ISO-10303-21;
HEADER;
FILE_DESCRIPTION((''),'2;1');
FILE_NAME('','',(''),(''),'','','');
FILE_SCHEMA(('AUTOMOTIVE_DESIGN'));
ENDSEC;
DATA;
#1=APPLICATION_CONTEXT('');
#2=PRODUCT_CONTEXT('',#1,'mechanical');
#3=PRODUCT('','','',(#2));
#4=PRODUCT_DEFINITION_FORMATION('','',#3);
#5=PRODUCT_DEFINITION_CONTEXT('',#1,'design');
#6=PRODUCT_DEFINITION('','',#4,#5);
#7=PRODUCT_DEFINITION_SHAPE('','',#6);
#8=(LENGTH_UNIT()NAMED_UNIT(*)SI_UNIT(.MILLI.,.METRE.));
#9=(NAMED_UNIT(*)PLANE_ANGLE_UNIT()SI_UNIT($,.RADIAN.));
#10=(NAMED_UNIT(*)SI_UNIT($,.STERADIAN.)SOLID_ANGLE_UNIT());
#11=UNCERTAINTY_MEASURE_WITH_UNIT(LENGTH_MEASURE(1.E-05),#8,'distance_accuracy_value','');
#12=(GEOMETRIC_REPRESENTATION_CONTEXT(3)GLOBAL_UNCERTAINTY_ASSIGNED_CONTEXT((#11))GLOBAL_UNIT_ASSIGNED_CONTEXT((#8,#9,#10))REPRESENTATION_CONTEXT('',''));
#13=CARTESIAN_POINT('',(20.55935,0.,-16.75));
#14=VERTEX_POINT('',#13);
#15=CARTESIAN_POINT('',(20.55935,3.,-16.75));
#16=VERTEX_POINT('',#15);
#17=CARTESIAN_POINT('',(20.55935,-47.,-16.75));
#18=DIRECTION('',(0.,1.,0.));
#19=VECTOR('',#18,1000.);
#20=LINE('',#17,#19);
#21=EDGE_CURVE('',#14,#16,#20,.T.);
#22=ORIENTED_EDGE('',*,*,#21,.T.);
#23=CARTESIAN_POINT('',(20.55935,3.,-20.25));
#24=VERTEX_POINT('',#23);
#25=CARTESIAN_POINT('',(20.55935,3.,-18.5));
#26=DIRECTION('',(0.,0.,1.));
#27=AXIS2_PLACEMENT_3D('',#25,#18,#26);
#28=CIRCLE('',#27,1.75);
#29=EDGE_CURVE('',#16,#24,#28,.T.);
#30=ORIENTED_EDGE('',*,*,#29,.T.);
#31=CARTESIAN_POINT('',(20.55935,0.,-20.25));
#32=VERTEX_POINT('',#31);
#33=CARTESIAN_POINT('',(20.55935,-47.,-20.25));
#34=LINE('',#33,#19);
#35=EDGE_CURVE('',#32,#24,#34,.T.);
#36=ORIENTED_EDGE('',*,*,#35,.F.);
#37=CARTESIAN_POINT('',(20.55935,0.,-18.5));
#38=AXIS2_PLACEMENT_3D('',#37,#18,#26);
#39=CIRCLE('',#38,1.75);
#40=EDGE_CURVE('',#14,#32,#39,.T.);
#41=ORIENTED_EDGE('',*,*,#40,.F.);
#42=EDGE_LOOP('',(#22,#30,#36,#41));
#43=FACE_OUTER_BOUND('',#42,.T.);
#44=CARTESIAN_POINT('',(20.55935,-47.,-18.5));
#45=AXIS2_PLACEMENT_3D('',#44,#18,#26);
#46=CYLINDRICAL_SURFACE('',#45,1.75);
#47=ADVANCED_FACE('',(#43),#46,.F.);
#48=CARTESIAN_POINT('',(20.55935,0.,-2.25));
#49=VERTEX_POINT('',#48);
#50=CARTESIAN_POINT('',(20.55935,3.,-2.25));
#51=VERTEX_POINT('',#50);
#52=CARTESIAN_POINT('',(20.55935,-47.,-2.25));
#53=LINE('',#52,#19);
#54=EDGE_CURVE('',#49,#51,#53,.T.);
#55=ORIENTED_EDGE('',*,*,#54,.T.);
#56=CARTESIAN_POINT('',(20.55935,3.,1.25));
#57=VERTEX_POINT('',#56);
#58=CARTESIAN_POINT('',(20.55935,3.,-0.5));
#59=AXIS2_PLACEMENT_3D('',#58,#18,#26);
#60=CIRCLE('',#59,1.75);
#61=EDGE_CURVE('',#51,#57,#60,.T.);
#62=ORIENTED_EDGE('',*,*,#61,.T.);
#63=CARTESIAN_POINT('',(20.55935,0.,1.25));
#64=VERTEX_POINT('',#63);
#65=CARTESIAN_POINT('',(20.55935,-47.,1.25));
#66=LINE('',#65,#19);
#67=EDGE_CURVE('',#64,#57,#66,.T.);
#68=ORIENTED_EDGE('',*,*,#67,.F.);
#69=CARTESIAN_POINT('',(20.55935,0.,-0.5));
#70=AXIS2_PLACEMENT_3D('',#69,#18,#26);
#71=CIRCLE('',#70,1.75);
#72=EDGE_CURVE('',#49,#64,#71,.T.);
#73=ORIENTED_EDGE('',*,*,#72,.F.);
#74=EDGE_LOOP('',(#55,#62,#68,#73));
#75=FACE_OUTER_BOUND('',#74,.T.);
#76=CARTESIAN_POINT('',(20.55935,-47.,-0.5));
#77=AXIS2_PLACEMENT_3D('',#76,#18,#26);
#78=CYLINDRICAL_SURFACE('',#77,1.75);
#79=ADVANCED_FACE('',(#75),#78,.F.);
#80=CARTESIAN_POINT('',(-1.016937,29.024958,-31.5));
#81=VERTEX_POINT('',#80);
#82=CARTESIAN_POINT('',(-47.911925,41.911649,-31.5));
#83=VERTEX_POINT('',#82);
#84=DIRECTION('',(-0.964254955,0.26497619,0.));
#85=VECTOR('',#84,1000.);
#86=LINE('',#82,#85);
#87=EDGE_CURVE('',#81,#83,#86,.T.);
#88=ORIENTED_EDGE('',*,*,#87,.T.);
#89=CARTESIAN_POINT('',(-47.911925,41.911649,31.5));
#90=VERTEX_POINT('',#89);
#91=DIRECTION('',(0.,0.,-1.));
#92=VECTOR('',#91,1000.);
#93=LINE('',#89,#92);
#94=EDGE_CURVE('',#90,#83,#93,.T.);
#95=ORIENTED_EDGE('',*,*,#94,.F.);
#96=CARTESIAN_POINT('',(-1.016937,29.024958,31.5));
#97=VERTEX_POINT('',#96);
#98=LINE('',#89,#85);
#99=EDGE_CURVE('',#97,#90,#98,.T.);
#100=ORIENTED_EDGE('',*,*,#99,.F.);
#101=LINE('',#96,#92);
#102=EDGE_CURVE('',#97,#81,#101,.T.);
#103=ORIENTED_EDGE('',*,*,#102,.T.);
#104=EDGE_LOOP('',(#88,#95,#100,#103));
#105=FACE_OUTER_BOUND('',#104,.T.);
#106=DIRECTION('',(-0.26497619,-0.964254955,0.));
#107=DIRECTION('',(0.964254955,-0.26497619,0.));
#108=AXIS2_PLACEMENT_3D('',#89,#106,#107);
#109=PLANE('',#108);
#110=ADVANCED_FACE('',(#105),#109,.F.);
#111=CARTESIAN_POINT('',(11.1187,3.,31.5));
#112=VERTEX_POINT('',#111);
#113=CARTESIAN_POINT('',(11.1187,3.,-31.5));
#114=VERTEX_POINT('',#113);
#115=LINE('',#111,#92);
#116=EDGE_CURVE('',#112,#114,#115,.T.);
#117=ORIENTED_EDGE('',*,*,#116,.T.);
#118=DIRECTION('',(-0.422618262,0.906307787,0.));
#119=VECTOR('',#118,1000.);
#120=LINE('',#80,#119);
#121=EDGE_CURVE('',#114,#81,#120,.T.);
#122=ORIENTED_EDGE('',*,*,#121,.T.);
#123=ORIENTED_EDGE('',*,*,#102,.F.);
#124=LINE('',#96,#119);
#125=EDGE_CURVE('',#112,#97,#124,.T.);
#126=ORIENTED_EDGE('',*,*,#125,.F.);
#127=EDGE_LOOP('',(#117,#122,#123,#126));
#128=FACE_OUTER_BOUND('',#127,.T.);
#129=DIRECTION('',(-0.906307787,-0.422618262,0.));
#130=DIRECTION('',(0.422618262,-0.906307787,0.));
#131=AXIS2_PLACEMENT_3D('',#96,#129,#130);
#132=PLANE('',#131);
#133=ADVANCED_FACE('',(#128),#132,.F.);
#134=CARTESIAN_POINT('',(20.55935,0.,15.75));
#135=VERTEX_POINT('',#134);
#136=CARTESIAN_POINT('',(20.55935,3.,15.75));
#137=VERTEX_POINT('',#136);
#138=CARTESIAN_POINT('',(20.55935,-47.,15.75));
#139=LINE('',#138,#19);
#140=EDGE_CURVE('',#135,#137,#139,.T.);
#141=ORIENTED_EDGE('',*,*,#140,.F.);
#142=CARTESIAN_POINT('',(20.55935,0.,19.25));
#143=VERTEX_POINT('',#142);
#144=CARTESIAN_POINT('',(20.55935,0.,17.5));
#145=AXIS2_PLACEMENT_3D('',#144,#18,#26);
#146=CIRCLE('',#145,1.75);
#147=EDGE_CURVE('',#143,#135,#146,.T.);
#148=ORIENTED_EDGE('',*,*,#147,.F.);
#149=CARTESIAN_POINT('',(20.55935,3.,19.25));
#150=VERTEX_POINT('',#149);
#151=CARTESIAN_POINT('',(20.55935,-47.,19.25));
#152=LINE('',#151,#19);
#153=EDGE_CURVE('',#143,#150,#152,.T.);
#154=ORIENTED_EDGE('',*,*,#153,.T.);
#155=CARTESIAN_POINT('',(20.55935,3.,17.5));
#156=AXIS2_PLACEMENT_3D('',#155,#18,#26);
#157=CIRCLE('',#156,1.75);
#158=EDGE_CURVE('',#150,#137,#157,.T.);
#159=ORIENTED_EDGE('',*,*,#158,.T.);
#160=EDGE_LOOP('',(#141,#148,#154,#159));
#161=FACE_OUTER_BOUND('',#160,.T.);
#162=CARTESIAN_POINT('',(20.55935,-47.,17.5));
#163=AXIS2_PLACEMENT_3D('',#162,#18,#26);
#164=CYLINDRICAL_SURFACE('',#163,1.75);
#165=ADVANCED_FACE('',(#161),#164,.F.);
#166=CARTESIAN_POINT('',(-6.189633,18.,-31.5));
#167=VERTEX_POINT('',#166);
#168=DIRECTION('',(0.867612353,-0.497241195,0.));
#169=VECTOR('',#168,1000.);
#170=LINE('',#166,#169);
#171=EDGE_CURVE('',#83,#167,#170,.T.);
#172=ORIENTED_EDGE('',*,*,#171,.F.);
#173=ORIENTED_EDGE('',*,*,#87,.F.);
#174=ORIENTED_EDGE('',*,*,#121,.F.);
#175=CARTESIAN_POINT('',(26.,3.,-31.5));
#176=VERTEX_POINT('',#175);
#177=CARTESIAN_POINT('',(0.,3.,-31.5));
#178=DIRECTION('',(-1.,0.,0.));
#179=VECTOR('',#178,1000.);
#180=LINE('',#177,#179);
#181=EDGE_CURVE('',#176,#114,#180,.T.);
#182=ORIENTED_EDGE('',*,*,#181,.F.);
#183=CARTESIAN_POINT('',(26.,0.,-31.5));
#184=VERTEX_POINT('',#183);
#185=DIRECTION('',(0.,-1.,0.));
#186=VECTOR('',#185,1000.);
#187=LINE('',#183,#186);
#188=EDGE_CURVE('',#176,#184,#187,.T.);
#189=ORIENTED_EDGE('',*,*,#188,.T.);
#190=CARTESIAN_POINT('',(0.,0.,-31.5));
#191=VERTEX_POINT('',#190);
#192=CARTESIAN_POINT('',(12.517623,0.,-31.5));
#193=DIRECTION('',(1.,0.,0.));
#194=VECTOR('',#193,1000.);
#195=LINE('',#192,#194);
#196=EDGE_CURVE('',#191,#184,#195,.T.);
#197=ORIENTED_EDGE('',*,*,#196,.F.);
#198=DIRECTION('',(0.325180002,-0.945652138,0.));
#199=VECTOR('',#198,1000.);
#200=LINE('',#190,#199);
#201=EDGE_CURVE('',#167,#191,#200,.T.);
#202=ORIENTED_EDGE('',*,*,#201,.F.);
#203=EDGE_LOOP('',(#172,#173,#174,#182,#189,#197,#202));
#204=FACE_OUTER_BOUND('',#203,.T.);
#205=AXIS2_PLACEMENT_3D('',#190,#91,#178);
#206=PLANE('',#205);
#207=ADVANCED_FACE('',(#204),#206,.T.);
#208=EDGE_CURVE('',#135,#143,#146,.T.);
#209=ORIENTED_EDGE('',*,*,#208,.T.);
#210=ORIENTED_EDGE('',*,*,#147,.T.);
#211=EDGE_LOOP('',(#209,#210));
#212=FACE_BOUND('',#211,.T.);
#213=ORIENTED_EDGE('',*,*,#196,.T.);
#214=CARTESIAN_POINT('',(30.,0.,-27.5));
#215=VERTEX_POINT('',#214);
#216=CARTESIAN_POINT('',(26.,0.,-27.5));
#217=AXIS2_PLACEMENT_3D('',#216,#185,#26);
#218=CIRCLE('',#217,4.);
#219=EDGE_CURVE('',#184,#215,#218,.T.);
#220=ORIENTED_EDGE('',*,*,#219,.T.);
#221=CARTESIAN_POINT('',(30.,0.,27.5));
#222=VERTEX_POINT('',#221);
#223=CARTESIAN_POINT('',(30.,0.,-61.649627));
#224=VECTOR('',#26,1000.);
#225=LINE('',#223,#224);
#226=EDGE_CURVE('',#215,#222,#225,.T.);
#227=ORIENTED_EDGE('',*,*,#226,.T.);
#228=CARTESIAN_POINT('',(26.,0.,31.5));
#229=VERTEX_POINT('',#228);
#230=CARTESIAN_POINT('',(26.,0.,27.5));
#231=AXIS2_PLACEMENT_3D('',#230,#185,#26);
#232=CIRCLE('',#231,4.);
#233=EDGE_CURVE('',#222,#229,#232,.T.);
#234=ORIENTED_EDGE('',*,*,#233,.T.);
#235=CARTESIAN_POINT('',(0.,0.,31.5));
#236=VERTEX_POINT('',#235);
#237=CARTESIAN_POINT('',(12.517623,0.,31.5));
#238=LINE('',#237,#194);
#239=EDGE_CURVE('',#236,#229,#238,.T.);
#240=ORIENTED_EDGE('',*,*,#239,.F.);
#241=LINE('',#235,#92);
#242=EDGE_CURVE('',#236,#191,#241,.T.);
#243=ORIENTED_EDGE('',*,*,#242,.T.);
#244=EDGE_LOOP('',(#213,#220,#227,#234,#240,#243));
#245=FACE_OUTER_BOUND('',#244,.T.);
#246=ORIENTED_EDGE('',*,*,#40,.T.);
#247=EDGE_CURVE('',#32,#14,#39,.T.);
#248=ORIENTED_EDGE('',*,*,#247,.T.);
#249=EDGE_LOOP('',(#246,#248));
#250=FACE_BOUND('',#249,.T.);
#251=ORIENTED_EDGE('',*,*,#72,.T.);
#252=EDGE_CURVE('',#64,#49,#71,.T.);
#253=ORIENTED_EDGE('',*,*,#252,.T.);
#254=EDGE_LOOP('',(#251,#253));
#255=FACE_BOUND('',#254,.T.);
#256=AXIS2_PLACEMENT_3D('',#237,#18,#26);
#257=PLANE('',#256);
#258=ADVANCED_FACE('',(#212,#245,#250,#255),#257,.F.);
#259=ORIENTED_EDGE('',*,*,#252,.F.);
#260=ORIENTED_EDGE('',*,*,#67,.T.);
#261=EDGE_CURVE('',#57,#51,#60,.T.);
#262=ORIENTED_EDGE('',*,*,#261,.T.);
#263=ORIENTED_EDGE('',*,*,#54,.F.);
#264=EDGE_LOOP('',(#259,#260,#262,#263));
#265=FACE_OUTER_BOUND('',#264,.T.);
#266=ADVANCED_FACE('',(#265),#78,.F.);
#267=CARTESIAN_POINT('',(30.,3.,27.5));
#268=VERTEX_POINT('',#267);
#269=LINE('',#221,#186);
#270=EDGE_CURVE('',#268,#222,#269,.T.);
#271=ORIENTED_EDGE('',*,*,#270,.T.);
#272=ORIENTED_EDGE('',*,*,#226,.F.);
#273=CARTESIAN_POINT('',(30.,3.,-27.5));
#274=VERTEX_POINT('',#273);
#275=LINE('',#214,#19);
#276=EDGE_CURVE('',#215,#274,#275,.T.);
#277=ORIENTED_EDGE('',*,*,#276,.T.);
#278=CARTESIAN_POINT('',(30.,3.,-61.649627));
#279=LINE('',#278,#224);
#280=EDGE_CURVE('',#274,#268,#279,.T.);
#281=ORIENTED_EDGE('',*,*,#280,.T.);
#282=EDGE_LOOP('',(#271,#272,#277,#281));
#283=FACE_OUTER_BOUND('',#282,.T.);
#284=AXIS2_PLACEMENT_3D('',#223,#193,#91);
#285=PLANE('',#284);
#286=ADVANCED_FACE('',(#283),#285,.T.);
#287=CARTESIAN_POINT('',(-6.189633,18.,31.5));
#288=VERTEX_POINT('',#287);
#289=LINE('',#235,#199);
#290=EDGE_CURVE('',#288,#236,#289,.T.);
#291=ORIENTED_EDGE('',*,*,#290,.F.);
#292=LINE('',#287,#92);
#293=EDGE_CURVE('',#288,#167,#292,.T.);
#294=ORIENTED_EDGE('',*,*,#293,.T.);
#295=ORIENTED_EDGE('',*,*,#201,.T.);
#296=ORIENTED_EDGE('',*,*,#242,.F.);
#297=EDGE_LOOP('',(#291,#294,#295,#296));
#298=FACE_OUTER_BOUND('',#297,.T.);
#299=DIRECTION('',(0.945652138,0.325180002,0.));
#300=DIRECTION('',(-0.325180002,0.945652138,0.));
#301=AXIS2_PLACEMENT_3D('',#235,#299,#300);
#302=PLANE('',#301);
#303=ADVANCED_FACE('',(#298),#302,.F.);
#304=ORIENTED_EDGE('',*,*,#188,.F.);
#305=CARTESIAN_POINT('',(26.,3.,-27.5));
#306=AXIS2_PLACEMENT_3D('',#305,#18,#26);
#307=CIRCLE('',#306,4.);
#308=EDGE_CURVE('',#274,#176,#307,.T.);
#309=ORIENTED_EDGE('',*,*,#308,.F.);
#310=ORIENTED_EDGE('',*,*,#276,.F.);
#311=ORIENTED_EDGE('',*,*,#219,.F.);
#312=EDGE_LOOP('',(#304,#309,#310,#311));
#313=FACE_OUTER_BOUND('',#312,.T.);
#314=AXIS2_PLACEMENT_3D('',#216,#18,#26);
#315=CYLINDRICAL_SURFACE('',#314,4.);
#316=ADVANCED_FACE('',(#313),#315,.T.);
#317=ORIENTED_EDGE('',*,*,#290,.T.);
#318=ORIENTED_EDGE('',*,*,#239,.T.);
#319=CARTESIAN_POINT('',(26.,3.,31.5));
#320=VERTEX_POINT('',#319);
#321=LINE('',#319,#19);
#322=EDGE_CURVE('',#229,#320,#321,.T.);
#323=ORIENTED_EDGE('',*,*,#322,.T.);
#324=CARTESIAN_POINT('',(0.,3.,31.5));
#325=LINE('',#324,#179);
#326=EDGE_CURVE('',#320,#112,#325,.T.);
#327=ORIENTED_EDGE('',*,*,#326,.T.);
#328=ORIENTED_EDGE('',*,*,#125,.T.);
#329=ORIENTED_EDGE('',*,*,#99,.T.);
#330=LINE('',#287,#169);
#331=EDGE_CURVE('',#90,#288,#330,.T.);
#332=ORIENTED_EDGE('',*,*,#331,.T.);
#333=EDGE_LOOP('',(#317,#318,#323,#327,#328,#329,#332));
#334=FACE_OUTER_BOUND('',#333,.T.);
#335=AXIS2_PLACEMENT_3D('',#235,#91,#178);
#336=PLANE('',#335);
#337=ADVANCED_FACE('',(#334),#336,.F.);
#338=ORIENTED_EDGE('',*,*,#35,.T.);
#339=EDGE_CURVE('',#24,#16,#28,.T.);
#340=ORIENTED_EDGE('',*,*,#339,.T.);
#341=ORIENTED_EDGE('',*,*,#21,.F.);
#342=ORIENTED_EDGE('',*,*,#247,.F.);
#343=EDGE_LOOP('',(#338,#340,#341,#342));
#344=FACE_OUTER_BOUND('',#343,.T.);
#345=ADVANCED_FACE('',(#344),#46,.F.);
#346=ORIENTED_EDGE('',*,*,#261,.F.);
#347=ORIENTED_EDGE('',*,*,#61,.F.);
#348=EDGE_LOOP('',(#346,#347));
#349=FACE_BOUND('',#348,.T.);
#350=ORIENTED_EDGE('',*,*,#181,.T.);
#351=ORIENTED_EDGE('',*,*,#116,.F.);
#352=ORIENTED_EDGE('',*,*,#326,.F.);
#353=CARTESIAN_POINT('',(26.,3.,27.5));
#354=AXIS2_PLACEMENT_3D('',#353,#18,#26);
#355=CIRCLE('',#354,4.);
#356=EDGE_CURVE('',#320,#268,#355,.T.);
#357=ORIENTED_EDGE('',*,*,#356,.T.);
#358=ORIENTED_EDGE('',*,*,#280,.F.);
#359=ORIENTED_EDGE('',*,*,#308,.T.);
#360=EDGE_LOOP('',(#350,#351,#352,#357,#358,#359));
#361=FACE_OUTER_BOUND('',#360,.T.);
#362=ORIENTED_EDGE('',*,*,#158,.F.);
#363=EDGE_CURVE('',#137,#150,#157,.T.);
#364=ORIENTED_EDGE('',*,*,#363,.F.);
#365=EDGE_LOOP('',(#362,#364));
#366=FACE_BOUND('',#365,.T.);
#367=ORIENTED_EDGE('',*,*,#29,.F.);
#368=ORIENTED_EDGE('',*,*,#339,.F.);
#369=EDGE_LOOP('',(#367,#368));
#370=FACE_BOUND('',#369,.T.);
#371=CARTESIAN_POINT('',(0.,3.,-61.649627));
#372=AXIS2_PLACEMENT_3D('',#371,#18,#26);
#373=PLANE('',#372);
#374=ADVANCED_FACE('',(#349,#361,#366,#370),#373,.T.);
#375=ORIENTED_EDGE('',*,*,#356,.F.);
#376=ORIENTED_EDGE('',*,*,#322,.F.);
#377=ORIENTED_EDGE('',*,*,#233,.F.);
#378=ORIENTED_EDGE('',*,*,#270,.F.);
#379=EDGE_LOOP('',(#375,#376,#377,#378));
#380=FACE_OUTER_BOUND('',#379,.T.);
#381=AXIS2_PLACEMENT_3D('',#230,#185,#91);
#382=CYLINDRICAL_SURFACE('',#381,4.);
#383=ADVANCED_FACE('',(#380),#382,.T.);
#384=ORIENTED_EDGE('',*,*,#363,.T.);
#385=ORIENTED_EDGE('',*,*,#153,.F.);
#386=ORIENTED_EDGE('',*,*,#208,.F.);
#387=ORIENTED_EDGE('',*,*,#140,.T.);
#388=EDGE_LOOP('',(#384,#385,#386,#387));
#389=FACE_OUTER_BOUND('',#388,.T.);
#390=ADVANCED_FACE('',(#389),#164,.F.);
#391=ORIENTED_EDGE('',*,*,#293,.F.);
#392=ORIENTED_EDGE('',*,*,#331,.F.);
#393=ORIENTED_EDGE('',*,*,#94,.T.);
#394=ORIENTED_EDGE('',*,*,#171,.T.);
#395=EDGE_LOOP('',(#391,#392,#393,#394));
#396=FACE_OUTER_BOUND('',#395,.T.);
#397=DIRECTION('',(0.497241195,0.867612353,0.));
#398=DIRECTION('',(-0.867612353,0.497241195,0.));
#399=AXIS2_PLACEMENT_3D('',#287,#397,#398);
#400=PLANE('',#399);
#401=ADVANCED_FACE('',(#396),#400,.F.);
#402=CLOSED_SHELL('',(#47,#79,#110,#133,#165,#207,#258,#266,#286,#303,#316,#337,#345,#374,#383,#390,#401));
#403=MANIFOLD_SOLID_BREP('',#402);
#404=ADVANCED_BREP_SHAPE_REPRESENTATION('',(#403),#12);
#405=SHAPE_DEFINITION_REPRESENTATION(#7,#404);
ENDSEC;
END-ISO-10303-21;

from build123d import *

# Parameters (mm, degrees)
BOSS_EXTRUDE1_DEPTH = 31.5
SKETCH2_W           = 30
SKETCH2_H           = 3
BOSS_EXTRUDE2_DEPTH = 63
SKETCH3_R           = 1.75
CUT_EXTRUDE1_DEPTH  = 50
FILLET1_R           = 4


with BuildPart() as part:
    # Sketch1 → Boss-Extrude1 (new, symmetric)
    with BuildSketch(Plane.XY):
        Polygon((0, 0), (-6.189633375, 18), (-47.911924672, 41.911648908), (-1.016937138, 29.024958443), (12.517623262, 0), align=None)
    extrude(amount=BOSS_EXTRUDE1_DEPTH, both=True)

    # Sketch2 → Boss-Extrude2 (add)
    with BuildSketch(Plane.XY.offset(31.5)):
        with Locations((15, 1.5)):
            Rectangle(SKETCH2_W, SKETCH2_H)
    extrude(amount=-BOSS_EXTRUDE2_DEPTH)

    # Sketch3 → Cut-Extrude1 (cut)
    with BuildSketch(Plane(origin=(0, 3, 0), x_dir=(1, 0, 0), z_dir=(0, 1, 0))):
        with Locations(Location((20.559350144, 18.5, 0), (0, 0, 270))):
            Circle(SKETCH3_R)
        with Locations(Location((20.559350144, 0.5, 0), (0, 0, 270))):
            Circle(SKETCH3_R)
        with Locations(Location((20.559350144, -17.5, 0), (0, 0, 270))):
            Circle(SKETCH3_R)
    extrude(amount=-CUT_EXTRUDE1_DEPTH, mode=Mode.SUBTRACT)

    # Fillet1
    fillet1_edges = [part.edges().sort_by_distance(p)[0] for p in [
        (30, 1.5, 31.5),
        (30, 1.5, -31.5),
    ]]
    fillet(fillet1_edges, radius=FILLET1_R)


solid = part.part
